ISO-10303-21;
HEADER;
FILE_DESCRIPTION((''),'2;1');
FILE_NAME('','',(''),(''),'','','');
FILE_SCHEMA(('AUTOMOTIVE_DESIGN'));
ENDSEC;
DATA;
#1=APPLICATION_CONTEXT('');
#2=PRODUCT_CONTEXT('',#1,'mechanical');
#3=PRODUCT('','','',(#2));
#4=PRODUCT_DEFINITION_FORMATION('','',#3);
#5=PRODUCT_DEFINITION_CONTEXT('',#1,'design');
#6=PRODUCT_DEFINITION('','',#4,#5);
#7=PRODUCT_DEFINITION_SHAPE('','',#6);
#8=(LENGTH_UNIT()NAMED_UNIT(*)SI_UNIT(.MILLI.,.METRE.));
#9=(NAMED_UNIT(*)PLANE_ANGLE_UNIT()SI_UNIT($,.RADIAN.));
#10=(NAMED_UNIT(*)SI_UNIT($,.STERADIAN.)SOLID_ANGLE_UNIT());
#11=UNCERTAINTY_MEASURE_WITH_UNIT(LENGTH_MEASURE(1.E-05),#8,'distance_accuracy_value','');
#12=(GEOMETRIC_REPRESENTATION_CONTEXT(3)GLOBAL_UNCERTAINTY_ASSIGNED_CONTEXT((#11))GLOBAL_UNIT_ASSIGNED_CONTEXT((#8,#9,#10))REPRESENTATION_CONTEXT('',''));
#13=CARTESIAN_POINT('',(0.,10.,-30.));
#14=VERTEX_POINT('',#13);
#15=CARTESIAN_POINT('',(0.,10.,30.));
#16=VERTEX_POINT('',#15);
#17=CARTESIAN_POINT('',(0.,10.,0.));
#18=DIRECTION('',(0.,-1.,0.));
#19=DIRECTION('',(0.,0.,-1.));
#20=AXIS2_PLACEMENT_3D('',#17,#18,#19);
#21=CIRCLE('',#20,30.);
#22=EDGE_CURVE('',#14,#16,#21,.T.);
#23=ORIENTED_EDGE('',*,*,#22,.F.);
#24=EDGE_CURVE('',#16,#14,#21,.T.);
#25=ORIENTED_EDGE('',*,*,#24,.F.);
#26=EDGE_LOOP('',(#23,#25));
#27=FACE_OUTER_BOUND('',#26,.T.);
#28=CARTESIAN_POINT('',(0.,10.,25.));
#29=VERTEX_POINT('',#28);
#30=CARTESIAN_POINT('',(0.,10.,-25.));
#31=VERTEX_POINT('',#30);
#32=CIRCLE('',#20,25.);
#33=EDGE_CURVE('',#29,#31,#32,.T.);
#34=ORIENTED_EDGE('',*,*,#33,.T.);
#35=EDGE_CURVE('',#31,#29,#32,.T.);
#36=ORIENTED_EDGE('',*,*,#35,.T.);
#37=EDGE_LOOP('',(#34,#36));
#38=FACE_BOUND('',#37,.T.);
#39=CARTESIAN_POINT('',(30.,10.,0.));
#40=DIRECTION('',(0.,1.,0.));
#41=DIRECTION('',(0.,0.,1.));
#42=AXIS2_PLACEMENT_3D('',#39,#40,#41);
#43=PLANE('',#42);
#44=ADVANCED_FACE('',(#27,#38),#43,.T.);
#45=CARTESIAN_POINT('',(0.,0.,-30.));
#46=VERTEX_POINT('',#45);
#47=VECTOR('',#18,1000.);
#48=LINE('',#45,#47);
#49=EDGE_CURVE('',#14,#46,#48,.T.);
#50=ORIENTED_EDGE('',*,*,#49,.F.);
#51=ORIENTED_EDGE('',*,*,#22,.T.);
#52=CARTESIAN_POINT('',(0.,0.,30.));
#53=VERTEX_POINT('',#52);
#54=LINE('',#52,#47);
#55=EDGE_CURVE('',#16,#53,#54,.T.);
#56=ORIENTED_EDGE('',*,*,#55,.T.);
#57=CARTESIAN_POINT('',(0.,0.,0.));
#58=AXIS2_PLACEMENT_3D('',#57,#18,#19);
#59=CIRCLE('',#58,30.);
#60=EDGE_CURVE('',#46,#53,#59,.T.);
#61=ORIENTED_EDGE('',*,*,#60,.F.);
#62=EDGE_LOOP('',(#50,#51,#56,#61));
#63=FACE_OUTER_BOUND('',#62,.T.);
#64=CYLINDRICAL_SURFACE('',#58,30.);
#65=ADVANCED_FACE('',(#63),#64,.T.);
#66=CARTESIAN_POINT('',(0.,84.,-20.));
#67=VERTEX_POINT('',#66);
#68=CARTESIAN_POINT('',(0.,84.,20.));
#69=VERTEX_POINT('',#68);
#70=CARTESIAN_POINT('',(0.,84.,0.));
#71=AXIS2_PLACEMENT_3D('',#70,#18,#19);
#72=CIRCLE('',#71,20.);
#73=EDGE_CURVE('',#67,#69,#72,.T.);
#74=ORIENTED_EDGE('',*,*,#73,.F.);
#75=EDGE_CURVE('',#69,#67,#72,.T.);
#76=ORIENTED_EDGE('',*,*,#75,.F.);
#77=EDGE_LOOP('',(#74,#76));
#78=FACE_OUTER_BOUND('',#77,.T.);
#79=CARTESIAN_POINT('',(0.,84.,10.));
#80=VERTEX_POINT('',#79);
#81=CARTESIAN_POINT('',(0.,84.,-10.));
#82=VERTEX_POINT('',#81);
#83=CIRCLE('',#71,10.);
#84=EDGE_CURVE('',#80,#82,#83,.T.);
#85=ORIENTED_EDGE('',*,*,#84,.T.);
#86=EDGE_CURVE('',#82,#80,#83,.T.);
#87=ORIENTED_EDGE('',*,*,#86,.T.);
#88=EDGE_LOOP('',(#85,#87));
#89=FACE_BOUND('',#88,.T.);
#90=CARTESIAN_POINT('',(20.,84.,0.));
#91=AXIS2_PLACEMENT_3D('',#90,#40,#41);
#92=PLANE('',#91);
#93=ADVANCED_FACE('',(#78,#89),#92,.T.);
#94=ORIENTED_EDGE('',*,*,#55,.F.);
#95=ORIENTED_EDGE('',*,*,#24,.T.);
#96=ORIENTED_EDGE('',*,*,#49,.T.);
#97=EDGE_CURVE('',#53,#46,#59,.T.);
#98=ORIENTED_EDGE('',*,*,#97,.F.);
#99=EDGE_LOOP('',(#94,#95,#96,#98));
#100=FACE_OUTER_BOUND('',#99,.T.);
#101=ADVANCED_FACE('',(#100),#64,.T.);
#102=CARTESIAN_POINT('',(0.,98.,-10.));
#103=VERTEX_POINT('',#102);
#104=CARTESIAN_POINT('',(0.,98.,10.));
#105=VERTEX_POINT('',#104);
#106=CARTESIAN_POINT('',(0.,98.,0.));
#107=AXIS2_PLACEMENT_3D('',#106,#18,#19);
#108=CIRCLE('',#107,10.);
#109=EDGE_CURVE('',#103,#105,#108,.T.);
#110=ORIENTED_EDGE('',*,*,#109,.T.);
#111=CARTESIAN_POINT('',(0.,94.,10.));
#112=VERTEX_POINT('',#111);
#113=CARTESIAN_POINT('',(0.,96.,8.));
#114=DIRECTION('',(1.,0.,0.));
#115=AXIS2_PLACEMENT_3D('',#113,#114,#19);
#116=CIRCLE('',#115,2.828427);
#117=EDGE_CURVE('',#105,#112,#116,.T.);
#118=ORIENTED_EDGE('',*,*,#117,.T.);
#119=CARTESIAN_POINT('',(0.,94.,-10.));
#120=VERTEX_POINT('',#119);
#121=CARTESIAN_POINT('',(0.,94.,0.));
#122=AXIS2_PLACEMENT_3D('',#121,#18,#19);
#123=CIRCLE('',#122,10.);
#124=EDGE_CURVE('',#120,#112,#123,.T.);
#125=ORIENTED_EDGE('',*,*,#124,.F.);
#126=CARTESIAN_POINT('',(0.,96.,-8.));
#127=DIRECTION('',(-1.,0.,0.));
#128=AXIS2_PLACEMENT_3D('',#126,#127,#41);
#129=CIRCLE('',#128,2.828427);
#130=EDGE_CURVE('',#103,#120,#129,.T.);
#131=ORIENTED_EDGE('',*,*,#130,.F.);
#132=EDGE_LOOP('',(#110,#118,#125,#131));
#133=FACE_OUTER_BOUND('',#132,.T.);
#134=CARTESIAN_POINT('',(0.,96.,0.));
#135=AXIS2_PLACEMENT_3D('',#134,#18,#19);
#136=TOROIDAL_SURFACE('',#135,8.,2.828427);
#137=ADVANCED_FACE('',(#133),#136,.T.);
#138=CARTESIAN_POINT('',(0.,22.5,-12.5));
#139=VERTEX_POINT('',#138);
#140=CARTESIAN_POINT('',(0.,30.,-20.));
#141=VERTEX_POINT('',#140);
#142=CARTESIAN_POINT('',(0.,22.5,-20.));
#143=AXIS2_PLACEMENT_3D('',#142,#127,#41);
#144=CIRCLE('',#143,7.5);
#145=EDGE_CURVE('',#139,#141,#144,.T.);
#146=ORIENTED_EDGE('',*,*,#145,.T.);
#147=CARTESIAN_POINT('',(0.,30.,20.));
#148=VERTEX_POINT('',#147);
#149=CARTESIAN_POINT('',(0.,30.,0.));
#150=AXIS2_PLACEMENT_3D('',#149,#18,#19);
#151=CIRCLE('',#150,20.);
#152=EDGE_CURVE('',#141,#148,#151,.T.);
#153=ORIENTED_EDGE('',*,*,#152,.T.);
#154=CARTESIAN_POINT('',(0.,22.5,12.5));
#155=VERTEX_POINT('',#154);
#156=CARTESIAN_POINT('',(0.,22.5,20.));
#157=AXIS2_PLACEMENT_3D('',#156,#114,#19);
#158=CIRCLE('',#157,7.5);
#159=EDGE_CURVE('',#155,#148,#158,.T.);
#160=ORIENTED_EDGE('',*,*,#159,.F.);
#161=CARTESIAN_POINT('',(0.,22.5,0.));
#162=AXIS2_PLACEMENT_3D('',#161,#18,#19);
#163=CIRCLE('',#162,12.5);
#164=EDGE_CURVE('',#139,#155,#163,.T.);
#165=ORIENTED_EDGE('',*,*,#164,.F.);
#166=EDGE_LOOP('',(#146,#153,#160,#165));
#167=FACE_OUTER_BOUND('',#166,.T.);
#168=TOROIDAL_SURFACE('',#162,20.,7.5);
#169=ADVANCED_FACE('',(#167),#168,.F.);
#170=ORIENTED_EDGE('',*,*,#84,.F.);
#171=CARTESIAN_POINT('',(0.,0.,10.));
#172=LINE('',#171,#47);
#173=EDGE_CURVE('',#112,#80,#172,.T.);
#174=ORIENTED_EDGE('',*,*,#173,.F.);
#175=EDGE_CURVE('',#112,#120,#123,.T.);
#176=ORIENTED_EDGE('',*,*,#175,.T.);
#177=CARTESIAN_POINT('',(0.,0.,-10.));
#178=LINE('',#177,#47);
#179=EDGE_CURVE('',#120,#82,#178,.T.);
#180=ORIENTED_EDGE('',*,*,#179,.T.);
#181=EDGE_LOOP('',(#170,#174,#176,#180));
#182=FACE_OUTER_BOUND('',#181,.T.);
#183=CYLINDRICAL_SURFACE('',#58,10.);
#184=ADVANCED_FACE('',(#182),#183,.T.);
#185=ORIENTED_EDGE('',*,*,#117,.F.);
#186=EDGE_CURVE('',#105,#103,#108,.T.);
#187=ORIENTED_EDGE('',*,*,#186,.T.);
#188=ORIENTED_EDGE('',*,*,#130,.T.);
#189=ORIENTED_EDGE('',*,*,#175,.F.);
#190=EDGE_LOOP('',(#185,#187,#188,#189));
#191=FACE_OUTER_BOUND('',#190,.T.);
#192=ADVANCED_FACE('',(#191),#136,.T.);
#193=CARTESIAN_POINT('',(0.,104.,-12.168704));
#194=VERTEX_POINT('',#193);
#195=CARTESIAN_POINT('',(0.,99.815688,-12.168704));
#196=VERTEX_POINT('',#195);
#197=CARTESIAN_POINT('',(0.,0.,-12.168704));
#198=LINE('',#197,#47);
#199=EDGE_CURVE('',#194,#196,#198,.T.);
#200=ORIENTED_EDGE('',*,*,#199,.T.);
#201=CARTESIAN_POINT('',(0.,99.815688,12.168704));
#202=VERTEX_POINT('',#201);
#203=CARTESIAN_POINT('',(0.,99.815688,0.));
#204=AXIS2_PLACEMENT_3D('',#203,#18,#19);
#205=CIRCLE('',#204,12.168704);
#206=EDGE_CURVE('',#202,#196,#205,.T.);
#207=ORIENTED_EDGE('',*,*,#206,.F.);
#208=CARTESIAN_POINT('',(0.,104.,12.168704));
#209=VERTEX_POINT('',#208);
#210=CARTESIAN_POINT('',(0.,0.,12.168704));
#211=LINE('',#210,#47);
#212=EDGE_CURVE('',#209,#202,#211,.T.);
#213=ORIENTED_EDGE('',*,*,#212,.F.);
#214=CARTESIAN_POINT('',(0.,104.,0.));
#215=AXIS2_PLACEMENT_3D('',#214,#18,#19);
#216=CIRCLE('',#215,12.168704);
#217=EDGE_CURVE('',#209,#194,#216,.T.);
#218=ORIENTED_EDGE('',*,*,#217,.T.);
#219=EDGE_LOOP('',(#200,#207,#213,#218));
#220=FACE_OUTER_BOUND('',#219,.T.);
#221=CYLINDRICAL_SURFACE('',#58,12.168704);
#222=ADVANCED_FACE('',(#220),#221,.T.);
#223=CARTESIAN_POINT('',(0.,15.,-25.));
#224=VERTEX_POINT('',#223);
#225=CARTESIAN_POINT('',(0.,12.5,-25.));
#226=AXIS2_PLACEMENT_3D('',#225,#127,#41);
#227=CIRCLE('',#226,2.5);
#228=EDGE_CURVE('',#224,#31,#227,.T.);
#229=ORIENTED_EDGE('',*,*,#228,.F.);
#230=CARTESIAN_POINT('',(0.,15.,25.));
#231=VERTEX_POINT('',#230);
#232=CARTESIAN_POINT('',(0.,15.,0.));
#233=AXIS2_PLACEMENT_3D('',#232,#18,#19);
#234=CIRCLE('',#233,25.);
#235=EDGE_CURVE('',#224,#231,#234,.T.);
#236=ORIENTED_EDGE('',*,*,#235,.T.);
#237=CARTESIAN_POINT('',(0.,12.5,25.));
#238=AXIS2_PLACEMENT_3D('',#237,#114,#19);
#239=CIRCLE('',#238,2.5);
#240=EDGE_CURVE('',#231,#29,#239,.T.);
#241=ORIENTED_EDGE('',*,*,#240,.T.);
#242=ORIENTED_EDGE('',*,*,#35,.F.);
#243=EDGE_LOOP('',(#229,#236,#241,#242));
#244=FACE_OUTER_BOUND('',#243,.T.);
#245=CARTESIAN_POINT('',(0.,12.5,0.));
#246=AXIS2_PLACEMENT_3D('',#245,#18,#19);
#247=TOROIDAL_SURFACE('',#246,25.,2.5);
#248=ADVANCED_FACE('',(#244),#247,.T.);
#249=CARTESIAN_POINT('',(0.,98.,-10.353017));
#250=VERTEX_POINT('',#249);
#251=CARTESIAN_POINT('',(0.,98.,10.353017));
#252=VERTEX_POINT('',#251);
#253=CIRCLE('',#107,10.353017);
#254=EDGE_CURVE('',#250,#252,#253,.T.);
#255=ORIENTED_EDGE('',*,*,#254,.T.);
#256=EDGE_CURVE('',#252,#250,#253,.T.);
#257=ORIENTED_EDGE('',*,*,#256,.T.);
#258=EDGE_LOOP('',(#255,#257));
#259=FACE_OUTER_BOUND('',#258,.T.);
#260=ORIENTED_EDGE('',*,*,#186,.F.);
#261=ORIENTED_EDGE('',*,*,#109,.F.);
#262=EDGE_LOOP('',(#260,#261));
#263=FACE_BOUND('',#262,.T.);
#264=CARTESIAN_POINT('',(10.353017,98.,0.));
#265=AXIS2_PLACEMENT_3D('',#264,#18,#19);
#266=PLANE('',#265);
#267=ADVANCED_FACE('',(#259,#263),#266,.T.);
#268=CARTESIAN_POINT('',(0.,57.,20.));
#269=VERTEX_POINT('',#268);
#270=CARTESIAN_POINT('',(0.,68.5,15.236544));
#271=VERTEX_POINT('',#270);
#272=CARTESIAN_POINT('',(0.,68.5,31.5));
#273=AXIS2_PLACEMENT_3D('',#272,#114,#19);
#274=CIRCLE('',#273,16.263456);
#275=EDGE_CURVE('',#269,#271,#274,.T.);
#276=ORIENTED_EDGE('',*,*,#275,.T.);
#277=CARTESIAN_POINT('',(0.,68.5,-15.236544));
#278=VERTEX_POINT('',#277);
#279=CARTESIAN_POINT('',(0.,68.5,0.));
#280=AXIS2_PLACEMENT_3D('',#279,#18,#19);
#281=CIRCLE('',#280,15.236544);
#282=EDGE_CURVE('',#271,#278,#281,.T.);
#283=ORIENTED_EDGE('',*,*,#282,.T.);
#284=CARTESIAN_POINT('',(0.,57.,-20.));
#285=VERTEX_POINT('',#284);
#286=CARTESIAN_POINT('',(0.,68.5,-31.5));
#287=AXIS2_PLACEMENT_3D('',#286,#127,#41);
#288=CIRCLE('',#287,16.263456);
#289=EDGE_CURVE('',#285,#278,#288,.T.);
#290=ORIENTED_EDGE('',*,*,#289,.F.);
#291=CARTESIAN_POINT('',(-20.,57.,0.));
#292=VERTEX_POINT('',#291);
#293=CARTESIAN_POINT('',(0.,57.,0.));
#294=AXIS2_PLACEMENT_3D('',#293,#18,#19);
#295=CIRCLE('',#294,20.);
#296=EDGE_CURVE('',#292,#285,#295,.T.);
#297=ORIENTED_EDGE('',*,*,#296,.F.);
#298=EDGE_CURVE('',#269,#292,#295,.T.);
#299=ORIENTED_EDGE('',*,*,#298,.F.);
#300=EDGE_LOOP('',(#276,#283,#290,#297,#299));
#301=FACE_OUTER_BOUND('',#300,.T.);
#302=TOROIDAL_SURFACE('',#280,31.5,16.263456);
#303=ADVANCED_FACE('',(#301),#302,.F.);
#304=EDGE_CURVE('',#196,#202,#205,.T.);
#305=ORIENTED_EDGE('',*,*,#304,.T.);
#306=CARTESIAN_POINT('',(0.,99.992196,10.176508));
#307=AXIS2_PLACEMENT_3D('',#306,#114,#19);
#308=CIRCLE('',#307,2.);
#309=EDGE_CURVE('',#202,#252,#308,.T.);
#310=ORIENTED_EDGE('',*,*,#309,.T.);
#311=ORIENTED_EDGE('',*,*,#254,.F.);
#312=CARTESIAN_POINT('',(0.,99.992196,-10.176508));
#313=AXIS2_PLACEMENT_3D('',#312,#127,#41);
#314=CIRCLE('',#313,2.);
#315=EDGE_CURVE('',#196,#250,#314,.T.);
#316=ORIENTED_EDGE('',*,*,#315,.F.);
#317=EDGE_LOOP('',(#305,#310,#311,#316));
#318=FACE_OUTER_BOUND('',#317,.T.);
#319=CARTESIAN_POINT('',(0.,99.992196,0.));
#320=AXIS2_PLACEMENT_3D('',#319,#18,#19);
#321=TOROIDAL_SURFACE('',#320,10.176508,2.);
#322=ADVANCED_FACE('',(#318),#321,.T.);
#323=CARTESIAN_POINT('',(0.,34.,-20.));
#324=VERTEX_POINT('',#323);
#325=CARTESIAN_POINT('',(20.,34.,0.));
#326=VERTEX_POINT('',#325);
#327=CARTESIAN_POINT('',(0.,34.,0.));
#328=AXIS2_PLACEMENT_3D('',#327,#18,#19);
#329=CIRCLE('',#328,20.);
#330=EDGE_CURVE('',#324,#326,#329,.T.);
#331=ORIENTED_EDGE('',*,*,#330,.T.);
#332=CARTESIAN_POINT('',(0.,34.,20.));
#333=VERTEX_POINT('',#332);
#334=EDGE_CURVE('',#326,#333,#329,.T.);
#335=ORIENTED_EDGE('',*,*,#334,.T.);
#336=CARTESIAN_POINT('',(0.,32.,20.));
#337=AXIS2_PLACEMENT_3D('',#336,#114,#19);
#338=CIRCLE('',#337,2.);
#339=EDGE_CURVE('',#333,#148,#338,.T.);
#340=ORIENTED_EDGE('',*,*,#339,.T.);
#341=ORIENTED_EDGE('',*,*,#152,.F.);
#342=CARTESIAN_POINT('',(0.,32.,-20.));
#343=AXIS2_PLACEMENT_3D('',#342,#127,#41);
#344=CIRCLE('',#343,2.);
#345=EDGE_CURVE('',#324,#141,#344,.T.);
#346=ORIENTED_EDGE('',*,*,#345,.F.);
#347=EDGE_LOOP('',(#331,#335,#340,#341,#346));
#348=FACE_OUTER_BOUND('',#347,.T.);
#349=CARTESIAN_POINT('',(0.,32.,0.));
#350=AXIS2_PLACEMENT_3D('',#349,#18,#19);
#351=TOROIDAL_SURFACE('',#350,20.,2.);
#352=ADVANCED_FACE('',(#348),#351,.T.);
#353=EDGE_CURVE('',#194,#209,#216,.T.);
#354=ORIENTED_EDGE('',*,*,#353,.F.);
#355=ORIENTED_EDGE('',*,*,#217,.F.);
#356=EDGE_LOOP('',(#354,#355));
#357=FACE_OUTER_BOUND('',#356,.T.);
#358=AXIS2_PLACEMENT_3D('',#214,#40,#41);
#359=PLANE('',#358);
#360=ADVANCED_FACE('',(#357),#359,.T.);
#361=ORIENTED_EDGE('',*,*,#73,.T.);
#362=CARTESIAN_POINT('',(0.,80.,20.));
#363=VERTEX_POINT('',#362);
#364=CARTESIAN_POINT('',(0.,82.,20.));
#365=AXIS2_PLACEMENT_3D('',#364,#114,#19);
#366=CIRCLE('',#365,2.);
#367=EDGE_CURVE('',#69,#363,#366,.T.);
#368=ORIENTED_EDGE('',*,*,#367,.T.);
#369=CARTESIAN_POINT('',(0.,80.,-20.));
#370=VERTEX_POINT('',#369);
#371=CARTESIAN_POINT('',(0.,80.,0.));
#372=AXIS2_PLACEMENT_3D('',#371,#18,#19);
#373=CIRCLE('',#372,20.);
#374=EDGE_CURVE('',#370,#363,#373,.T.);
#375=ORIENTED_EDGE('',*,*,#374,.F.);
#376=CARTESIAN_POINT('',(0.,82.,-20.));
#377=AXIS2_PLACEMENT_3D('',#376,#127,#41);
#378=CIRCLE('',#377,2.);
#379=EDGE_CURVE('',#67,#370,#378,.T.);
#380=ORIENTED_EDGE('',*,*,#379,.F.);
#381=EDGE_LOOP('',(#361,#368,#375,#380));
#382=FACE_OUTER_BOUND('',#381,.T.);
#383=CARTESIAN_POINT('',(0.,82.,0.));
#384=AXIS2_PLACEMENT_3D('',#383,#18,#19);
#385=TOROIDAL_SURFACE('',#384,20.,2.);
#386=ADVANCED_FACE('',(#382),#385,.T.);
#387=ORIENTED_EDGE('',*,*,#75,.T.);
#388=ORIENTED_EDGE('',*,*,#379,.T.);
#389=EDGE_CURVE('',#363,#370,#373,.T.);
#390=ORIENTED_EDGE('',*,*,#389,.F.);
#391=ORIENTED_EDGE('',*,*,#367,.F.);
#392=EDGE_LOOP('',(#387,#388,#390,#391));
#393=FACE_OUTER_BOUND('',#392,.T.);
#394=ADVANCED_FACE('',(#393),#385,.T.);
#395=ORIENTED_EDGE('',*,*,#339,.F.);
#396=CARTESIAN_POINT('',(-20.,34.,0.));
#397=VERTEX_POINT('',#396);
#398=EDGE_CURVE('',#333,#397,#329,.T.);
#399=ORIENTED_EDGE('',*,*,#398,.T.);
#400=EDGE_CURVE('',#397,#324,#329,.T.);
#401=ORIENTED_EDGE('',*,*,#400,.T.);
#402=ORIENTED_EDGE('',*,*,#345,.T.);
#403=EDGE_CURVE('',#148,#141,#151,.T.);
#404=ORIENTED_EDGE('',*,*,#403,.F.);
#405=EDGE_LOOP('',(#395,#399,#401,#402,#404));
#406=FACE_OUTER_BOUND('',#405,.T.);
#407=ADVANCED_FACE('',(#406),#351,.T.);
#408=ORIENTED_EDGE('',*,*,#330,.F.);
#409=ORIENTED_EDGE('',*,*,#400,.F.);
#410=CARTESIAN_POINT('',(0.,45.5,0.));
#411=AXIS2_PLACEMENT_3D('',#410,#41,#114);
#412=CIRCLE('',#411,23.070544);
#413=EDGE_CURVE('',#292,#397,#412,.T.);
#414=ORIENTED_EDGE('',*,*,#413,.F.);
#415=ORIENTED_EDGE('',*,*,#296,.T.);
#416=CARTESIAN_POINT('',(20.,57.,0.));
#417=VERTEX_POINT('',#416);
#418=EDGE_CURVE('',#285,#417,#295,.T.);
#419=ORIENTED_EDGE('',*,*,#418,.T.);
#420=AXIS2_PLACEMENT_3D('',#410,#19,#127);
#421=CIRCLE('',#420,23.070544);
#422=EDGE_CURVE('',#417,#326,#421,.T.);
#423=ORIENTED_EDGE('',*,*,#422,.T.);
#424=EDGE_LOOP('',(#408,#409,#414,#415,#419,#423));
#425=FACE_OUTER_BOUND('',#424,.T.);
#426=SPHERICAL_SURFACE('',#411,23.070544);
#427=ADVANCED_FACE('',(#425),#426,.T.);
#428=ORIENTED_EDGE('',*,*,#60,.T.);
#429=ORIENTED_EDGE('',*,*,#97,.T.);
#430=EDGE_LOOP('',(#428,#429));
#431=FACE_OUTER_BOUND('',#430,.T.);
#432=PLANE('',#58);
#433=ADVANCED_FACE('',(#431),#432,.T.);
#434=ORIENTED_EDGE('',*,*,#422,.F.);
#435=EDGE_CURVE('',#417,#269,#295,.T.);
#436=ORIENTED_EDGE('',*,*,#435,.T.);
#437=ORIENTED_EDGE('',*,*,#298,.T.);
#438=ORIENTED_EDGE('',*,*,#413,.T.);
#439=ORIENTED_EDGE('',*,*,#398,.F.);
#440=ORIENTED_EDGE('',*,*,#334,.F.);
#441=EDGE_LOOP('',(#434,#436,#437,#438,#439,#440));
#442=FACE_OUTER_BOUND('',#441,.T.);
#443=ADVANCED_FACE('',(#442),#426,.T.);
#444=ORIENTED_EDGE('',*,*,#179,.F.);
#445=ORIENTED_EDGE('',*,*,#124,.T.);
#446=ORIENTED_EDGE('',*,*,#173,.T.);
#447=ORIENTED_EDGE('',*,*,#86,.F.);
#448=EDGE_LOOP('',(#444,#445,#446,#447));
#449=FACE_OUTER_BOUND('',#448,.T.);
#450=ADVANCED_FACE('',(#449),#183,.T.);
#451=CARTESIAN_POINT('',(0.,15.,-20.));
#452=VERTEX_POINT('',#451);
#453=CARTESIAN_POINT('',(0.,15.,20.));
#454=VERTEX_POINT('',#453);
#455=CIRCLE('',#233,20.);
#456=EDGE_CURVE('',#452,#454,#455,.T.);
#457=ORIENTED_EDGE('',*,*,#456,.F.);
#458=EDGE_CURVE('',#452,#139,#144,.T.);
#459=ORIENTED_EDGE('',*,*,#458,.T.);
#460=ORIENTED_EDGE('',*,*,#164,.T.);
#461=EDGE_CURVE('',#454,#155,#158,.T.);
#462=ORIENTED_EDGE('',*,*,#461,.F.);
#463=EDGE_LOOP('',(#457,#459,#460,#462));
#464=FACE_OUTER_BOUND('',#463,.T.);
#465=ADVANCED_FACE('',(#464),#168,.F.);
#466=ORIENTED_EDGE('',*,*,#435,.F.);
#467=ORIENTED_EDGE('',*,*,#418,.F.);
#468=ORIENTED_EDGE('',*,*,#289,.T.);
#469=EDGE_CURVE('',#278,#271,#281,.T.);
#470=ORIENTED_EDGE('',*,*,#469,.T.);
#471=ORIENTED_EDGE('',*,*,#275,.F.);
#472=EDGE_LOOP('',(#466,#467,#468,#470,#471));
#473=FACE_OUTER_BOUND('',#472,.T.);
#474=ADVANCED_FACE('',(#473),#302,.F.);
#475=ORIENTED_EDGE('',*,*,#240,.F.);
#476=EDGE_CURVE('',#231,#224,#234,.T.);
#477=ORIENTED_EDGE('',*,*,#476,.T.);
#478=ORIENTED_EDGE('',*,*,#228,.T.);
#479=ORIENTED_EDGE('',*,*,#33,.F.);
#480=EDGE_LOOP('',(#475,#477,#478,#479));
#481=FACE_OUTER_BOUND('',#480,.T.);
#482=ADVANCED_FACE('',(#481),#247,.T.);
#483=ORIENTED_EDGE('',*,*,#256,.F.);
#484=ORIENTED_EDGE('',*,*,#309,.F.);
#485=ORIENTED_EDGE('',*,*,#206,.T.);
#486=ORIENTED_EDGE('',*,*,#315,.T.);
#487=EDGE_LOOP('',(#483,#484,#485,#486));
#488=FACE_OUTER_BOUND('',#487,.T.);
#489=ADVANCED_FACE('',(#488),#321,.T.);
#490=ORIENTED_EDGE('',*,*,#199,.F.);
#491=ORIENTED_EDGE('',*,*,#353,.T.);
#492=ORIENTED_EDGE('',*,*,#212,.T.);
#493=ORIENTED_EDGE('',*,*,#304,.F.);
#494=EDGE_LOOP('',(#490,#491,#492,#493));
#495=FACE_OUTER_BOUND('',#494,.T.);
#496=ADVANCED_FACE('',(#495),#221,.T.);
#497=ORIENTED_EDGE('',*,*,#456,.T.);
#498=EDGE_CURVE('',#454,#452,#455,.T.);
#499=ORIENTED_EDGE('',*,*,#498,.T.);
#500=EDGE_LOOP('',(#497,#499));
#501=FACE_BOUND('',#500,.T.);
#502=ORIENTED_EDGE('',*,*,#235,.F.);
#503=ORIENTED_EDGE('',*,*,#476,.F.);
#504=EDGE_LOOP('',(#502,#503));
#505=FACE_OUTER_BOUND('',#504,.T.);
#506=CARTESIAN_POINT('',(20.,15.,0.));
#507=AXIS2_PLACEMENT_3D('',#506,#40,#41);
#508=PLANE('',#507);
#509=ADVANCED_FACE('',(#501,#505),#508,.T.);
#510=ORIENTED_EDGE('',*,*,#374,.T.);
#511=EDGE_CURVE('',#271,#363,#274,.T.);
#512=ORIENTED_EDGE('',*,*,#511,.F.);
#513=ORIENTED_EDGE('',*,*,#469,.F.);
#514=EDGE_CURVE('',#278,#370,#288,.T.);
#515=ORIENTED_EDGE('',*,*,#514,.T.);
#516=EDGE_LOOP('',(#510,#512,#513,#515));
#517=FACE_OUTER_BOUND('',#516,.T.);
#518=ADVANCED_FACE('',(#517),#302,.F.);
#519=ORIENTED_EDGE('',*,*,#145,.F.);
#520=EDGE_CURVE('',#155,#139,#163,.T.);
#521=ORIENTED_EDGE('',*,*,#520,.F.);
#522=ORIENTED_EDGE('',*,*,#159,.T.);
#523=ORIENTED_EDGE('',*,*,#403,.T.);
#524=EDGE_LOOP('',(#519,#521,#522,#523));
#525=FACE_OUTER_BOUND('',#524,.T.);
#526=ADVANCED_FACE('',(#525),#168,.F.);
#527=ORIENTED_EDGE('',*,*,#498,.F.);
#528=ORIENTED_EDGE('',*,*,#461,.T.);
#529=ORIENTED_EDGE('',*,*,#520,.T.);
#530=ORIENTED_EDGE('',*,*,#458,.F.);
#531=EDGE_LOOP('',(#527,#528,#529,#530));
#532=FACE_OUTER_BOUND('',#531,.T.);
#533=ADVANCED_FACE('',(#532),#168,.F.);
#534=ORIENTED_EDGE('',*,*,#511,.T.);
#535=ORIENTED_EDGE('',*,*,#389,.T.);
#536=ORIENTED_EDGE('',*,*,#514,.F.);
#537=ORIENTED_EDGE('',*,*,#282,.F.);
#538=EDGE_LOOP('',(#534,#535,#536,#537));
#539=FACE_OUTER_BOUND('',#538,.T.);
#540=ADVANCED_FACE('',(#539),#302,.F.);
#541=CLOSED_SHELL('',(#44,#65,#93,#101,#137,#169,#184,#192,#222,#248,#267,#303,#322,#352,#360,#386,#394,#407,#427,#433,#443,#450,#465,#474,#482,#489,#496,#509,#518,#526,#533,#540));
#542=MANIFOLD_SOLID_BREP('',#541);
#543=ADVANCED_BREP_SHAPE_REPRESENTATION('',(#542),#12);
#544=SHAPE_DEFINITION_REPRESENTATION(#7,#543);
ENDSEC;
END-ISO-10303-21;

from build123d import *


with BuildPart() as part:
    # Baluster Half Profile → Baluster Body Revolve 360° (revolve)
    with BuildSketch(Plane.XY, mode=Mode.PRIVATE) as baluster_body_revolve_360_sk:
        with BuildLine():
            Line((0, 0), (30, 0))
            Line((30, 0), (30, 10))
            Line((30, 10), (25, 10))
            ThreePointArc((25, 10), (27.5, 12.5), (25, 15))
            Line((25, 15), (20, 15))
            ThreePointArc((20, 15), (12.5, 22.5), (20, 30))
            ThreePointArc((20, 30), (22, 32), (20, 34))
            ThreePointArc((20, 34), (23.07054399, 45.5), (20, 57))
            ThreePointArc((20, 57), (15.236544033, 68.5), (20, 80))
            ThreePointArc((20, 80), (22, 82), (20, 84))
            Line((20, 84), (10, 84))
            Line((10, 84), (10, 94))
            ThreePointArc((10, 94), (10.828427125, 96), (10, 98))
            Line((10, 98), (10.353016606, 98))
            ThreePointArc((10.353016606, 98), (11.590721865, 98.577982417), (12.168704282, 99.815687676))
            Line((12.168704282, 99.815687676), (12.168704282, 104))
            Line((12.168704282, 104), (0, 104))
            Line((0, 104), (0, 0))
        make_face()
    revolve(baluster_body_revolve_360_sk.sketch.rotate(Axis((0, 0, 0), (0, 1, 0)), 90), axis=Axis((0, 0, 0), (0, 1, 0)))


solid = part.part
